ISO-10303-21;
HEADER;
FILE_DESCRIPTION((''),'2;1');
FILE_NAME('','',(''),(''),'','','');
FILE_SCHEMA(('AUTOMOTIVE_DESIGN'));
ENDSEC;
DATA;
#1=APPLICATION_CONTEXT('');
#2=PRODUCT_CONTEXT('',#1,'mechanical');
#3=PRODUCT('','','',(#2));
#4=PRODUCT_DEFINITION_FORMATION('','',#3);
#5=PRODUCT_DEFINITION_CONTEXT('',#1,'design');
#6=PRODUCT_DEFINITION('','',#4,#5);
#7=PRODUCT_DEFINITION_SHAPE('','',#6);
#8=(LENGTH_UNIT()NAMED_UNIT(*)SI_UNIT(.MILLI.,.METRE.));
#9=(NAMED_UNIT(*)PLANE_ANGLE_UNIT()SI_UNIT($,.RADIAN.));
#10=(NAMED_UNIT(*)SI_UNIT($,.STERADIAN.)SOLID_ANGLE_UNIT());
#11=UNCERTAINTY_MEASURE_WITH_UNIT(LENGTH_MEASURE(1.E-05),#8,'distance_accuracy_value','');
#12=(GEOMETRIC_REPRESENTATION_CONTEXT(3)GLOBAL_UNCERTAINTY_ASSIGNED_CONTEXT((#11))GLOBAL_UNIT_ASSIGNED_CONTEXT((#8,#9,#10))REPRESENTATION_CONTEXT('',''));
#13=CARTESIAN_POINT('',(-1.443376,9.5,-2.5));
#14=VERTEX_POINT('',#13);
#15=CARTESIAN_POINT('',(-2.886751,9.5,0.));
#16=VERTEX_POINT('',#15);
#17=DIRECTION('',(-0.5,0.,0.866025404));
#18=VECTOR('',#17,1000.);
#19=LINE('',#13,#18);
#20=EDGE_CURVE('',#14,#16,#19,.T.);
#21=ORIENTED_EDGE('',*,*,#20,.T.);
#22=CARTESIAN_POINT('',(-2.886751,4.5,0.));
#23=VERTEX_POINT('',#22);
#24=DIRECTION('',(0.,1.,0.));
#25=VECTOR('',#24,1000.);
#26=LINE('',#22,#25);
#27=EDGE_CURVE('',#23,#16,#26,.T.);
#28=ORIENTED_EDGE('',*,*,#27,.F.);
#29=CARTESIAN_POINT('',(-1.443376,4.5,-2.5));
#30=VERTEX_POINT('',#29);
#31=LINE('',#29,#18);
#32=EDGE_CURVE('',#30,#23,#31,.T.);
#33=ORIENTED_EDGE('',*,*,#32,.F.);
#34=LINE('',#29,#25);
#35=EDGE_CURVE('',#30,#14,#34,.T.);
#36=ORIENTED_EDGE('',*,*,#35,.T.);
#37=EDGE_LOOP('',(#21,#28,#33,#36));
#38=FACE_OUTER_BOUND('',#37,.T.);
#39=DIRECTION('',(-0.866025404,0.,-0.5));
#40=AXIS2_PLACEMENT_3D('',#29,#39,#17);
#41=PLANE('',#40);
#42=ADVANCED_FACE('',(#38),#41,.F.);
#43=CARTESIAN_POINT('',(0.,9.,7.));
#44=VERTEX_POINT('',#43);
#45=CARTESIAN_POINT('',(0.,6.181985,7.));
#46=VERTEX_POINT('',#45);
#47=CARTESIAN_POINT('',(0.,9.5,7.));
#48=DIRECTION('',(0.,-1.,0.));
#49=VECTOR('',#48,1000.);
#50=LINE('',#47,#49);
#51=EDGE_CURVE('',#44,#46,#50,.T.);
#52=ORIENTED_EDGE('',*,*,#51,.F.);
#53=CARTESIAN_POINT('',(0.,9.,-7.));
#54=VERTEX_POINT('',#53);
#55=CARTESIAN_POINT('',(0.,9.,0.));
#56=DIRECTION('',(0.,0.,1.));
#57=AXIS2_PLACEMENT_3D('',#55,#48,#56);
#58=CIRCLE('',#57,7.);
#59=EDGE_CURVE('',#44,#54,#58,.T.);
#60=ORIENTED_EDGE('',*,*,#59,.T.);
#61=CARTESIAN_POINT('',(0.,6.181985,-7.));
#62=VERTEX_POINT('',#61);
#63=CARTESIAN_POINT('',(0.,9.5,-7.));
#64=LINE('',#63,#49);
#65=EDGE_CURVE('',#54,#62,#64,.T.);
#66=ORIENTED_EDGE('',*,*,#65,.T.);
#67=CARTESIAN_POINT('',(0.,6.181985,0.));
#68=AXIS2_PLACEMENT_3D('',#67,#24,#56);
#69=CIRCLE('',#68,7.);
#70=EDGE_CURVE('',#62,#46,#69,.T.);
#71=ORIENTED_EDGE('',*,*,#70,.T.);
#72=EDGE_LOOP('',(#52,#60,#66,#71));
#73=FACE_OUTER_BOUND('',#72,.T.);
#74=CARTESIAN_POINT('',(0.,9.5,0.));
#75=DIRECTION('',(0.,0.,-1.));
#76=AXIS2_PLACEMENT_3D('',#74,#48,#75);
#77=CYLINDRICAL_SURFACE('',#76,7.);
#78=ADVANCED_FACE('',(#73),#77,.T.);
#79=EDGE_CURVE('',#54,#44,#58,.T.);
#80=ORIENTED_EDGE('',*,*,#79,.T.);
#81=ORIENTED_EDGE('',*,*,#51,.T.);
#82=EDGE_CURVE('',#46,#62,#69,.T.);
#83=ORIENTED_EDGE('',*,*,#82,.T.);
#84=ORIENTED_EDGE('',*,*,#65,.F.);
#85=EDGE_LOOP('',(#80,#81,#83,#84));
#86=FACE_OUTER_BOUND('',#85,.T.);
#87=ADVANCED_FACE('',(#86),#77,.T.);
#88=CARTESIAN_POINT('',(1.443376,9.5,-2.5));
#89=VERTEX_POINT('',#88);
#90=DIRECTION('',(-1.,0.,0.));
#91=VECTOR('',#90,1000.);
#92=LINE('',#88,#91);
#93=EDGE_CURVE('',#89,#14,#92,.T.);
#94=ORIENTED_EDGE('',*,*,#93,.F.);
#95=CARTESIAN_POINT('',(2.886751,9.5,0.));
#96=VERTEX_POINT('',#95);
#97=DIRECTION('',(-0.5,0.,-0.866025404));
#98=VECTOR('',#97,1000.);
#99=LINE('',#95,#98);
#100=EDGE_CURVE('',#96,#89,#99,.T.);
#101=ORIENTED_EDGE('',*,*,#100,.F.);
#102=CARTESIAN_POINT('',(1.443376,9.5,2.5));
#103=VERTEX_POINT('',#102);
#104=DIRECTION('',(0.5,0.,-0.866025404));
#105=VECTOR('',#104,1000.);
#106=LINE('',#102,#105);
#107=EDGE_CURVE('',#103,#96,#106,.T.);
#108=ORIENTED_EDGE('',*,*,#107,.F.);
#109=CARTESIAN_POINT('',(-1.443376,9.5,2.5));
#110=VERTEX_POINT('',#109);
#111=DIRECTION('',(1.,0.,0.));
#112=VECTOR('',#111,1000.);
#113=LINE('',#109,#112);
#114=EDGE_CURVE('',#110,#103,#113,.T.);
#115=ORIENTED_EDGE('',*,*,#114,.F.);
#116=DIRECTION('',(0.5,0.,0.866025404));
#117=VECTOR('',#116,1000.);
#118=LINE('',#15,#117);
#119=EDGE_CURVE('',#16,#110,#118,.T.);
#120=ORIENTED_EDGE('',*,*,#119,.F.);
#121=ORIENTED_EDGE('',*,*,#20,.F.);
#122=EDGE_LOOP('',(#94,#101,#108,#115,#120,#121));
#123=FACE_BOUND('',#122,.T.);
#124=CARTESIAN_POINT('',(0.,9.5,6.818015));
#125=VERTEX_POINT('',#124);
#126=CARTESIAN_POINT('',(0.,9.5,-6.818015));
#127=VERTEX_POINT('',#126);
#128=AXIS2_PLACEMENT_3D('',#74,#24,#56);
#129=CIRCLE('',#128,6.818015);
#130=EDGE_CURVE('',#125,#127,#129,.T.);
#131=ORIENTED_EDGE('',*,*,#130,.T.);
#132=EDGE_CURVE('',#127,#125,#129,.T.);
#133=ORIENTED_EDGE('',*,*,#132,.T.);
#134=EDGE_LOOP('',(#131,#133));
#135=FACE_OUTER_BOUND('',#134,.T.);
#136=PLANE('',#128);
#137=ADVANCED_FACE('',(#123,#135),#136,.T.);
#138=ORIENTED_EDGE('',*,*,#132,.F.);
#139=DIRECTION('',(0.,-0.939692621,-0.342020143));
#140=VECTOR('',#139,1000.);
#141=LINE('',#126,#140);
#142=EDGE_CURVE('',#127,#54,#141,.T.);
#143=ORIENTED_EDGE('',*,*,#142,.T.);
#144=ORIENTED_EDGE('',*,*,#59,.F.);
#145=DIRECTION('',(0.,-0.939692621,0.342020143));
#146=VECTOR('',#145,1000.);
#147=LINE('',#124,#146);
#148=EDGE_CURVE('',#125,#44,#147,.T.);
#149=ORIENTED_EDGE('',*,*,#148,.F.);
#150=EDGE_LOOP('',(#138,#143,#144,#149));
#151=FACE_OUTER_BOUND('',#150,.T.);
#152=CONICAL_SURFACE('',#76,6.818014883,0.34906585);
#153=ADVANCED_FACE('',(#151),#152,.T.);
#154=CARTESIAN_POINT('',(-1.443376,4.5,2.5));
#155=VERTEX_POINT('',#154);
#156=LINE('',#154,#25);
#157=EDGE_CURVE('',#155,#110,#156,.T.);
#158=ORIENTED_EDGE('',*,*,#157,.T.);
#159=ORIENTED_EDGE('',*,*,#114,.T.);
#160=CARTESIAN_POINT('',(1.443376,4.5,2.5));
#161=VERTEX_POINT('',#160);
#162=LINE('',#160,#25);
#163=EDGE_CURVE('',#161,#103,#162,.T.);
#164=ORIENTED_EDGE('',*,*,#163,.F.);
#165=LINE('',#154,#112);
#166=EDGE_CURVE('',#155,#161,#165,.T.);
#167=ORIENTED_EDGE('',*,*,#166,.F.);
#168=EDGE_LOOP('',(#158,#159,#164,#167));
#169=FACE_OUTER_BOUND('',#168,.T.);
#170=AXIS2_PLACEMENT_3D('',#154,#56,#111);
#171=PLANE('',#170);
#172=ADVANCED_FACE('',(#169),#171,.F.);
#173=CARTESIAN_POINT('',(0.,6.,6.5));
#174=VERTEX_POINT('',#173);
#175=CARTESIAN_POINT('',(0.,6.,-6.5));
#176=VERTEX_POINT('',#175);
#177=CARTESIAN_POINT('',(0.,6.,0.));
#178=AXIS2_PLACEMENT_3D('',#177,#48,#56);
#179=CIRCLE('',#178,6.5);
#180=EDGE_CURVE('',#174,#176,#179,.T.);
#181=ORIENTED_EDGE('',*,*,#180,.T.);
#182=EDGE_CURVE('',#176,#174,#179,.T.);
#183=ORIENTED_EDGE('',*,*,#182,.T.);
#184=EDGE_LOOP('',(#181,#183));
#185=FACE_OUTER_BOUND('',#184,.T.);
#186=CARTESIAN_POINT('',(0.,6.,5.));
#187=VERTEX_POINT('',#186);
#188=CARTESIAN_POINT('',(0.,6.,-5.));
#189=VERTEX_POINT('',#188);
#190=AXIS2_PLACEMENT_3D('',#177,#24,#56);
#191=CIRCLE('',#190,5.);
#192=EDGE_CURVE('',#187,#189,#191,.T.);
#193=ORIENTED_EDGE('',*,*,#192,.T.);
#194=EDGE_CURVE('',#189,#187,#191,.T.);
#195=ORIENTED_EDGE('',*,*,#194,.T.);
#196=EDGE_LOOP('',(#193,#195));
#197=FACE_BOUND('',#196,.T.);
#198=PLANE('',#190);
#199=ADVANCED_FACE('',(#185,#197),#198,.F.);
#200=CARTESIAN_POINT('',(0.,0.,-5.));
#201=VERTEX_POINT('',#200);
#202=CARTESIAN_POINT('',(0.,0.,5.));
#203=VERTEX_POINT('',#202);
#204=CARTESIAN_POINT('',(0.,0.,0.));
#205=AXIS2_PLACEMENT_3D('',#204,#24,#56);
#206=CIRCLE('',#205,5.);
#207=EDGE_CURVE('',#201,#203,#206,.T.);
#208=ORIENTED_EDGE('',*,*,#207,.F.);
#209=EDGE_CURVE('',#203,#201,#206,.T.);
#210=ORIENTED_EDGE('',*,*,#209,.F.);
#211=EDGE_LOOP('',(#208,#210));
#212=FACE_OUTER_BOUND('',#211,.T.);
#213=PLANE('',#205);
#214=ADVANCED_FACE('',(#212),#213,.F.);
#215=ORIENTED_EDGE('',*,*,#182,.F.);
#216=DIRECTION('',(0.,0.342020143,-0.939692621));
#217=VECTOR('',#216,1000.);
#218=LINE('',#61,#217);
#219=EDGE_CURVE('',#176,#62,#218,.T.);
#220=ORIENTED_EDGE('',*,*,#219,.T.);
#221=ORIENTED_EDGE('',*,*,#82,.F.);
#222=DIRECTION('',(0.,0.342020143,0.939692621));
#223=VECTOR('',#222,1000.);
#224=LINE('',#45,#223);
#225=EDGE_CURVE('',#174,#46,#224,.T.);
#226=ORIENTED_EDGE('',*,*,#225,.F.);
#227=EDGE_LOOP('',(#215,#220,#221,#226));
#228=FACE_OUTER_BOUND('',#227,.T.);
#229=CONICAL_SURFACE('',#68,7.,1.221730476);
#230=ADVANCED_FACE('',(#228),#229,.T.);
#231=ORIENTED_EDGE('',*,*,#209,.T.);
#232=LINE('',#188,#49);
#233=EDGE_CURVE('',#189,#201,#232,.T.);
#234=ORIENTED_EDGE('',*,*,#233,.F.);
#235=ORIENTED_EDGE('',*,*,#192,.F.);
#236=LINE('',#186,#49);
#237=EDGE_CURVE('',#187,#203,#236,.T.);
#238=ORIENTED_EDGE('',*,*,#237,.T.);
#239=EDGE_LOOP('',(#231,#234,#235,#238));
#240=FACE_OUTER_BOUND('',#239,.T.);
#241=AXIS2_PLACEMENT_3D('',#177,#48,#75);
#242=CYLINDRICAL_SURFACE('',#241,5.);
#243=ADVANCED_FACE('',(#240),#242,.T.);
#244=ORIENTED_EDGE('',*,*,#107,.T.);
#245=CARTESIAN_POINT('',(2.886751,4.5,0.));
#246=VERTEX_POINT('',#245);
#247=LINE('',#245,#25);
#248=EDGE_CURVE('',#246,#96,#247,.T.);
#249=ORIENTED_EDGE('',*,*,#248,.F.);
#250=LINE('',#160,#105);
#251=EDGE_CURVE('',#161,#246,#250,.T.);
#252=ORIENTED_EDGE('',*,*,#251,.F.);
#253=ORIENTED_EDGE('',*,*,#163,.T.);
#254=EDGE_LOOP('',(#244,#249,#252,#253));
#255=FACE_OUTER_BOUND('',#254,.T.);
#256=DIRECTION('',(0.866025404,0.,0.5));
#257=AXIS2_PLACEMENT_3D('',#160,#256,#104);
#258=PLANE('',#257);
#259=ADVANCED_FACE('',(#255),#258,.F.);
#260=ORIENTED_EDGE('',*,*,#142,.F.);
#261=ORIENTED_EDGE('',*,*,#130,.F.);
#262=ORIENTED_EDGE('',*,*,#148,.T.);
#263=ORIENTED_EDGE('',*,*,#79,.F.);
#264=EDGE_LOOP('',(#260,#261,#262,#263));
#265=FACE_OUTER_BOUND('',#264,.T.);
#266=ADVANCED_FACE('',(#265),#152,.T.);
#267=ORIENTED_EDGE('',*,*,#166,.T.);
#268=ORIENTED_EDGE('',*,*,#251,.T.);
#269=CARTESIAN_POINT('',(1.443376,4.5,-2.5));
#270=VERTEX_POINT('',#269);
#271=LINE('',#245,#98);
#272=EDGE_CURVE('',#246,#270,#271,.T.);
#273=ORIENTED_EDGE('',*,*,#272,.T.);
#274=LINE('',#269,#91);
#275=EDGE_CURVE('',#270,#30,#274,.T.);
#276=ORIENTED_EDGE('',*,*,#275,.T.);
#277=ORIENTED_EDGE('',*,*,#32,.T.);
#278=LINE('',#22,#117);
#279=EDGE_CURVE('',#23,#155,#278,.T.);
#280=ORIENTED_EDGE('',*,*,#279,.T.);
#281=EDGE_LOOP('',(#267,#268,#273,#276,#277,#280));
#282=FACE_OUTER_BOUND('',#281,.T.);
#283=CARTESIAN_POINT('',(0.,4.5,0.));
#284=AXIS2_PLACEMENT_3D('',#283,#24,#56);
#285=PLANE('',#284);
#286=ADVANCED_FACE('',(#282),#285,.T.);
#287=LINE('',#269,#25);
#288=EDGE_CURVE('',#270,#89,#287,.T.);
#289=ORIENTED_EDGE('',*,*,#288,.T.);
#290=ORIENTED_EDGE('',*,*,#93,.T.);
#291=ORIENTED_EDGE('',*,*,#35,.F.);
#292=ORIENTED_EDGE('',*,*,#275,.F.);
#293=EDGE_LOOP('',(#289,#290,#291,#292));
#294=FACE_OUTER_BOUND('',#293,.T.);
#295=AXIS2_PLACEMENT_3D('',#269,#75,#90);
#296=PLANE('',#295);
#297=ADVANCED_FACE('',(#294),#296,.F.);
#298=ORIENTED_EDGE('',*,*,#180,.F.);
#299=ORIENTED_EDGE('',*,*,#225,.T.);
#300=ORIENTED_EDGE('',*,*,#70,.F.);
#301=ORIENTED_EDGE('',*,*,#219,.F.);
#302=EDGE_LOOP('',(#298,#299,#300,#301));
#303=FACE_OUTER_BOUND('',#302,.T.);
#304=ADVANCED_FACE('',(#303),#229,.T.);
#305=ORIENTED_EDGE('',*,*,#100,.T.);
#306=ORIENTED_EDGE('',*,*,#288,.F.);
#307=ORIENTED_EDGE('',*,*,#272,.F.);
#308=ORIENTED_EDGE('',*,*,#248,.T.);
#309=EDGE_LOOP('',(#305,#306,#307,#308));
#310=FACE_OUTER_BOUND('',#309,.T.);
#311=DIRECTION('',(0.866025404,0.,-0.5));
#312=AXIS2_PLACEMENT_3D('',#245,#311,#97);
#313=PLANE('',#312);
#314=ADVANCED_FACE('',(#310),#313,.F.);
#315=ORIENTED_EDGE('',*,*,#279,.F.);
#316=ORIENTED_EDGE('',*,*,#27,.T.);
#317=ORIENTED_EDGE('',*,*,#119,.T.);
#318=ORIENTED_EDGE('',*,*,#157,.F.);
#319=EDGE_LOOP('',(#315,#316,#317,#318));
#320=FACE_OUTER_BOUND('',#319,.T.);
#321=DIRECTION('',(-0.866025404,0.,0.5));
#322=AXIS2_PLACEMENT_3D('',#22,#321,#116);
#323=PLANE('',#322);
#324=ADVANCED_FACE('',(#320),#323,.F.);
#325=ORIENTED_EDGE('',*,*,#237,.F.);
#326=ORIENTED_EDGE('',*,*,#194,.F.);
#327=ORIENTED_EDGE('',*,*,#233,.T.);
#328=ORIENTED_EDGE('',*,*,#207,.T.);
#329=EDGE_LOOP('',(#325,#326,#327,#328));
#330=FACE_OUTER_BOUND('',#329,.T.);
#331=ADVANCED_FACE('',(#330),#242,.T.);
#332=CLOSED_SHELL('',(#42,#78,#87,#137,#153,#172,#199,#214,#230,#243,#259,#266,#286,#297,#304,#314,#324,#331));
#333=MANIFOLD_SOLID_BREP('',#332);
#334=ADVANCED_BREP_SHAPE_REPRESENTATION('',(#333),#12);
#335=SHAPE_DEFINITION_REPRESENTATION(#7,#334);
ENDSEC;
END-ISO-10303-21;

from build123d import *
from OCP.BRepFilletAPI import BRepFilletAPI_MakeChamfer

# Parameters (mm, degrees)
SKETCH1_R           = 5
BOSS_EXTRUDE1_DEPTH = 6
SKETCH3_R           = 7
BOSS_EXTRUDE2_DEPTH = 3.5
CUT_EXTRUDE1_DEPTH  = 5
CHAMFER1_SIZE       = 0.5
CHAMFER1_SIZE2      = 0.181985117


with BuildPart() as part:
    # Sketch1 → Boss-Extrude1 (new body)
    with BuildSketch(Plane(origin=(0, 0, 0), x_dir=(1, 0, 0), z_dir=(0, 1, 0))):
        with Locations(Location((0, 0, 0), (0, 0, 270))):
            Circle(SKETCH1_R)
    extrude(amount=BOSS_EXTRUDE1_DEPTH)

    # Sketch3 → Boss-Extrude2 (add)
    with BuildSketch(Plane(origin=(0, 6, 0), x_dir=(1, 0, 0), z_dir=(0, 1, 0))):
        with Locations(Location((0, 0, 0), (0, 0, 270))):
            Circle(SKETCH3_R)
    extrude(amount=BOSS_EXTRUDE2_DEPTH)

    # Sketch4 → Cut-Extrude1 (cut)
    with BuildSketch(Plane(origin=(0, 9.5, 0), x_dir=(1, 0, 0), z_dir=(0, 1, 0))):
        Polygon((-2.886751346, 0), (-1.443375673, -2.5), (1.443375673, -2.5), (2.886751346, 0), (1.443375673, 2.5), (-1.443375673, 2.5), align=None)
    extrude(amount=-CUT_EXTRUDE1_DEPTH, mode=Mode.SUBTRACT)

    # Chamfer1: one chamfer whose edges measure the first distance from different faces: ONE call of the kernel's chamfer builder (chamfer() names one face for all edges)
    chamfer1_edges_1 = [part.edges().sort_by_distance(p)[0] for p in [
        (0, 6, -7),
    ]]
    chamfer1_side_1 = [part.faces().sort_by_distance(p)[0] for p in [
        (0, 6, -6.802010101),
    ]]
    chamfer1_edges_2 = [part.edges().sort_by_distance(p)[0] for p in [
        (0, 9.5, -7),
    ]]
    chamfer1_side_2 = [part.faces().sort_by_distance(p)[0] for p in [
        (0, 7.75, -7),
    ]]
    chamfer1 = BRepFilletAPI_MakeChamfer(part.part.solid().wrapped)
    for e in chamfer1_edges_1:
        chamfer1.Add(CHAMFER1_SIZE, CHAMFER1_SIZE2, e.wrapped, chamfer1_side_1[0].wrapped)  # the first distance lies on this face
    for e in chamfer1_edges_2:
        chamfer1.Add(CHAMFER1_SIZE, CHAMFER1_SIZE2, e.wrapped, chamfer1_side_2[0].wrapped)  # the first distance lies on this face
    add(Compound.cast(chamfer1.Shape()), mode=Mode.REPLACE)


solid = part.part
